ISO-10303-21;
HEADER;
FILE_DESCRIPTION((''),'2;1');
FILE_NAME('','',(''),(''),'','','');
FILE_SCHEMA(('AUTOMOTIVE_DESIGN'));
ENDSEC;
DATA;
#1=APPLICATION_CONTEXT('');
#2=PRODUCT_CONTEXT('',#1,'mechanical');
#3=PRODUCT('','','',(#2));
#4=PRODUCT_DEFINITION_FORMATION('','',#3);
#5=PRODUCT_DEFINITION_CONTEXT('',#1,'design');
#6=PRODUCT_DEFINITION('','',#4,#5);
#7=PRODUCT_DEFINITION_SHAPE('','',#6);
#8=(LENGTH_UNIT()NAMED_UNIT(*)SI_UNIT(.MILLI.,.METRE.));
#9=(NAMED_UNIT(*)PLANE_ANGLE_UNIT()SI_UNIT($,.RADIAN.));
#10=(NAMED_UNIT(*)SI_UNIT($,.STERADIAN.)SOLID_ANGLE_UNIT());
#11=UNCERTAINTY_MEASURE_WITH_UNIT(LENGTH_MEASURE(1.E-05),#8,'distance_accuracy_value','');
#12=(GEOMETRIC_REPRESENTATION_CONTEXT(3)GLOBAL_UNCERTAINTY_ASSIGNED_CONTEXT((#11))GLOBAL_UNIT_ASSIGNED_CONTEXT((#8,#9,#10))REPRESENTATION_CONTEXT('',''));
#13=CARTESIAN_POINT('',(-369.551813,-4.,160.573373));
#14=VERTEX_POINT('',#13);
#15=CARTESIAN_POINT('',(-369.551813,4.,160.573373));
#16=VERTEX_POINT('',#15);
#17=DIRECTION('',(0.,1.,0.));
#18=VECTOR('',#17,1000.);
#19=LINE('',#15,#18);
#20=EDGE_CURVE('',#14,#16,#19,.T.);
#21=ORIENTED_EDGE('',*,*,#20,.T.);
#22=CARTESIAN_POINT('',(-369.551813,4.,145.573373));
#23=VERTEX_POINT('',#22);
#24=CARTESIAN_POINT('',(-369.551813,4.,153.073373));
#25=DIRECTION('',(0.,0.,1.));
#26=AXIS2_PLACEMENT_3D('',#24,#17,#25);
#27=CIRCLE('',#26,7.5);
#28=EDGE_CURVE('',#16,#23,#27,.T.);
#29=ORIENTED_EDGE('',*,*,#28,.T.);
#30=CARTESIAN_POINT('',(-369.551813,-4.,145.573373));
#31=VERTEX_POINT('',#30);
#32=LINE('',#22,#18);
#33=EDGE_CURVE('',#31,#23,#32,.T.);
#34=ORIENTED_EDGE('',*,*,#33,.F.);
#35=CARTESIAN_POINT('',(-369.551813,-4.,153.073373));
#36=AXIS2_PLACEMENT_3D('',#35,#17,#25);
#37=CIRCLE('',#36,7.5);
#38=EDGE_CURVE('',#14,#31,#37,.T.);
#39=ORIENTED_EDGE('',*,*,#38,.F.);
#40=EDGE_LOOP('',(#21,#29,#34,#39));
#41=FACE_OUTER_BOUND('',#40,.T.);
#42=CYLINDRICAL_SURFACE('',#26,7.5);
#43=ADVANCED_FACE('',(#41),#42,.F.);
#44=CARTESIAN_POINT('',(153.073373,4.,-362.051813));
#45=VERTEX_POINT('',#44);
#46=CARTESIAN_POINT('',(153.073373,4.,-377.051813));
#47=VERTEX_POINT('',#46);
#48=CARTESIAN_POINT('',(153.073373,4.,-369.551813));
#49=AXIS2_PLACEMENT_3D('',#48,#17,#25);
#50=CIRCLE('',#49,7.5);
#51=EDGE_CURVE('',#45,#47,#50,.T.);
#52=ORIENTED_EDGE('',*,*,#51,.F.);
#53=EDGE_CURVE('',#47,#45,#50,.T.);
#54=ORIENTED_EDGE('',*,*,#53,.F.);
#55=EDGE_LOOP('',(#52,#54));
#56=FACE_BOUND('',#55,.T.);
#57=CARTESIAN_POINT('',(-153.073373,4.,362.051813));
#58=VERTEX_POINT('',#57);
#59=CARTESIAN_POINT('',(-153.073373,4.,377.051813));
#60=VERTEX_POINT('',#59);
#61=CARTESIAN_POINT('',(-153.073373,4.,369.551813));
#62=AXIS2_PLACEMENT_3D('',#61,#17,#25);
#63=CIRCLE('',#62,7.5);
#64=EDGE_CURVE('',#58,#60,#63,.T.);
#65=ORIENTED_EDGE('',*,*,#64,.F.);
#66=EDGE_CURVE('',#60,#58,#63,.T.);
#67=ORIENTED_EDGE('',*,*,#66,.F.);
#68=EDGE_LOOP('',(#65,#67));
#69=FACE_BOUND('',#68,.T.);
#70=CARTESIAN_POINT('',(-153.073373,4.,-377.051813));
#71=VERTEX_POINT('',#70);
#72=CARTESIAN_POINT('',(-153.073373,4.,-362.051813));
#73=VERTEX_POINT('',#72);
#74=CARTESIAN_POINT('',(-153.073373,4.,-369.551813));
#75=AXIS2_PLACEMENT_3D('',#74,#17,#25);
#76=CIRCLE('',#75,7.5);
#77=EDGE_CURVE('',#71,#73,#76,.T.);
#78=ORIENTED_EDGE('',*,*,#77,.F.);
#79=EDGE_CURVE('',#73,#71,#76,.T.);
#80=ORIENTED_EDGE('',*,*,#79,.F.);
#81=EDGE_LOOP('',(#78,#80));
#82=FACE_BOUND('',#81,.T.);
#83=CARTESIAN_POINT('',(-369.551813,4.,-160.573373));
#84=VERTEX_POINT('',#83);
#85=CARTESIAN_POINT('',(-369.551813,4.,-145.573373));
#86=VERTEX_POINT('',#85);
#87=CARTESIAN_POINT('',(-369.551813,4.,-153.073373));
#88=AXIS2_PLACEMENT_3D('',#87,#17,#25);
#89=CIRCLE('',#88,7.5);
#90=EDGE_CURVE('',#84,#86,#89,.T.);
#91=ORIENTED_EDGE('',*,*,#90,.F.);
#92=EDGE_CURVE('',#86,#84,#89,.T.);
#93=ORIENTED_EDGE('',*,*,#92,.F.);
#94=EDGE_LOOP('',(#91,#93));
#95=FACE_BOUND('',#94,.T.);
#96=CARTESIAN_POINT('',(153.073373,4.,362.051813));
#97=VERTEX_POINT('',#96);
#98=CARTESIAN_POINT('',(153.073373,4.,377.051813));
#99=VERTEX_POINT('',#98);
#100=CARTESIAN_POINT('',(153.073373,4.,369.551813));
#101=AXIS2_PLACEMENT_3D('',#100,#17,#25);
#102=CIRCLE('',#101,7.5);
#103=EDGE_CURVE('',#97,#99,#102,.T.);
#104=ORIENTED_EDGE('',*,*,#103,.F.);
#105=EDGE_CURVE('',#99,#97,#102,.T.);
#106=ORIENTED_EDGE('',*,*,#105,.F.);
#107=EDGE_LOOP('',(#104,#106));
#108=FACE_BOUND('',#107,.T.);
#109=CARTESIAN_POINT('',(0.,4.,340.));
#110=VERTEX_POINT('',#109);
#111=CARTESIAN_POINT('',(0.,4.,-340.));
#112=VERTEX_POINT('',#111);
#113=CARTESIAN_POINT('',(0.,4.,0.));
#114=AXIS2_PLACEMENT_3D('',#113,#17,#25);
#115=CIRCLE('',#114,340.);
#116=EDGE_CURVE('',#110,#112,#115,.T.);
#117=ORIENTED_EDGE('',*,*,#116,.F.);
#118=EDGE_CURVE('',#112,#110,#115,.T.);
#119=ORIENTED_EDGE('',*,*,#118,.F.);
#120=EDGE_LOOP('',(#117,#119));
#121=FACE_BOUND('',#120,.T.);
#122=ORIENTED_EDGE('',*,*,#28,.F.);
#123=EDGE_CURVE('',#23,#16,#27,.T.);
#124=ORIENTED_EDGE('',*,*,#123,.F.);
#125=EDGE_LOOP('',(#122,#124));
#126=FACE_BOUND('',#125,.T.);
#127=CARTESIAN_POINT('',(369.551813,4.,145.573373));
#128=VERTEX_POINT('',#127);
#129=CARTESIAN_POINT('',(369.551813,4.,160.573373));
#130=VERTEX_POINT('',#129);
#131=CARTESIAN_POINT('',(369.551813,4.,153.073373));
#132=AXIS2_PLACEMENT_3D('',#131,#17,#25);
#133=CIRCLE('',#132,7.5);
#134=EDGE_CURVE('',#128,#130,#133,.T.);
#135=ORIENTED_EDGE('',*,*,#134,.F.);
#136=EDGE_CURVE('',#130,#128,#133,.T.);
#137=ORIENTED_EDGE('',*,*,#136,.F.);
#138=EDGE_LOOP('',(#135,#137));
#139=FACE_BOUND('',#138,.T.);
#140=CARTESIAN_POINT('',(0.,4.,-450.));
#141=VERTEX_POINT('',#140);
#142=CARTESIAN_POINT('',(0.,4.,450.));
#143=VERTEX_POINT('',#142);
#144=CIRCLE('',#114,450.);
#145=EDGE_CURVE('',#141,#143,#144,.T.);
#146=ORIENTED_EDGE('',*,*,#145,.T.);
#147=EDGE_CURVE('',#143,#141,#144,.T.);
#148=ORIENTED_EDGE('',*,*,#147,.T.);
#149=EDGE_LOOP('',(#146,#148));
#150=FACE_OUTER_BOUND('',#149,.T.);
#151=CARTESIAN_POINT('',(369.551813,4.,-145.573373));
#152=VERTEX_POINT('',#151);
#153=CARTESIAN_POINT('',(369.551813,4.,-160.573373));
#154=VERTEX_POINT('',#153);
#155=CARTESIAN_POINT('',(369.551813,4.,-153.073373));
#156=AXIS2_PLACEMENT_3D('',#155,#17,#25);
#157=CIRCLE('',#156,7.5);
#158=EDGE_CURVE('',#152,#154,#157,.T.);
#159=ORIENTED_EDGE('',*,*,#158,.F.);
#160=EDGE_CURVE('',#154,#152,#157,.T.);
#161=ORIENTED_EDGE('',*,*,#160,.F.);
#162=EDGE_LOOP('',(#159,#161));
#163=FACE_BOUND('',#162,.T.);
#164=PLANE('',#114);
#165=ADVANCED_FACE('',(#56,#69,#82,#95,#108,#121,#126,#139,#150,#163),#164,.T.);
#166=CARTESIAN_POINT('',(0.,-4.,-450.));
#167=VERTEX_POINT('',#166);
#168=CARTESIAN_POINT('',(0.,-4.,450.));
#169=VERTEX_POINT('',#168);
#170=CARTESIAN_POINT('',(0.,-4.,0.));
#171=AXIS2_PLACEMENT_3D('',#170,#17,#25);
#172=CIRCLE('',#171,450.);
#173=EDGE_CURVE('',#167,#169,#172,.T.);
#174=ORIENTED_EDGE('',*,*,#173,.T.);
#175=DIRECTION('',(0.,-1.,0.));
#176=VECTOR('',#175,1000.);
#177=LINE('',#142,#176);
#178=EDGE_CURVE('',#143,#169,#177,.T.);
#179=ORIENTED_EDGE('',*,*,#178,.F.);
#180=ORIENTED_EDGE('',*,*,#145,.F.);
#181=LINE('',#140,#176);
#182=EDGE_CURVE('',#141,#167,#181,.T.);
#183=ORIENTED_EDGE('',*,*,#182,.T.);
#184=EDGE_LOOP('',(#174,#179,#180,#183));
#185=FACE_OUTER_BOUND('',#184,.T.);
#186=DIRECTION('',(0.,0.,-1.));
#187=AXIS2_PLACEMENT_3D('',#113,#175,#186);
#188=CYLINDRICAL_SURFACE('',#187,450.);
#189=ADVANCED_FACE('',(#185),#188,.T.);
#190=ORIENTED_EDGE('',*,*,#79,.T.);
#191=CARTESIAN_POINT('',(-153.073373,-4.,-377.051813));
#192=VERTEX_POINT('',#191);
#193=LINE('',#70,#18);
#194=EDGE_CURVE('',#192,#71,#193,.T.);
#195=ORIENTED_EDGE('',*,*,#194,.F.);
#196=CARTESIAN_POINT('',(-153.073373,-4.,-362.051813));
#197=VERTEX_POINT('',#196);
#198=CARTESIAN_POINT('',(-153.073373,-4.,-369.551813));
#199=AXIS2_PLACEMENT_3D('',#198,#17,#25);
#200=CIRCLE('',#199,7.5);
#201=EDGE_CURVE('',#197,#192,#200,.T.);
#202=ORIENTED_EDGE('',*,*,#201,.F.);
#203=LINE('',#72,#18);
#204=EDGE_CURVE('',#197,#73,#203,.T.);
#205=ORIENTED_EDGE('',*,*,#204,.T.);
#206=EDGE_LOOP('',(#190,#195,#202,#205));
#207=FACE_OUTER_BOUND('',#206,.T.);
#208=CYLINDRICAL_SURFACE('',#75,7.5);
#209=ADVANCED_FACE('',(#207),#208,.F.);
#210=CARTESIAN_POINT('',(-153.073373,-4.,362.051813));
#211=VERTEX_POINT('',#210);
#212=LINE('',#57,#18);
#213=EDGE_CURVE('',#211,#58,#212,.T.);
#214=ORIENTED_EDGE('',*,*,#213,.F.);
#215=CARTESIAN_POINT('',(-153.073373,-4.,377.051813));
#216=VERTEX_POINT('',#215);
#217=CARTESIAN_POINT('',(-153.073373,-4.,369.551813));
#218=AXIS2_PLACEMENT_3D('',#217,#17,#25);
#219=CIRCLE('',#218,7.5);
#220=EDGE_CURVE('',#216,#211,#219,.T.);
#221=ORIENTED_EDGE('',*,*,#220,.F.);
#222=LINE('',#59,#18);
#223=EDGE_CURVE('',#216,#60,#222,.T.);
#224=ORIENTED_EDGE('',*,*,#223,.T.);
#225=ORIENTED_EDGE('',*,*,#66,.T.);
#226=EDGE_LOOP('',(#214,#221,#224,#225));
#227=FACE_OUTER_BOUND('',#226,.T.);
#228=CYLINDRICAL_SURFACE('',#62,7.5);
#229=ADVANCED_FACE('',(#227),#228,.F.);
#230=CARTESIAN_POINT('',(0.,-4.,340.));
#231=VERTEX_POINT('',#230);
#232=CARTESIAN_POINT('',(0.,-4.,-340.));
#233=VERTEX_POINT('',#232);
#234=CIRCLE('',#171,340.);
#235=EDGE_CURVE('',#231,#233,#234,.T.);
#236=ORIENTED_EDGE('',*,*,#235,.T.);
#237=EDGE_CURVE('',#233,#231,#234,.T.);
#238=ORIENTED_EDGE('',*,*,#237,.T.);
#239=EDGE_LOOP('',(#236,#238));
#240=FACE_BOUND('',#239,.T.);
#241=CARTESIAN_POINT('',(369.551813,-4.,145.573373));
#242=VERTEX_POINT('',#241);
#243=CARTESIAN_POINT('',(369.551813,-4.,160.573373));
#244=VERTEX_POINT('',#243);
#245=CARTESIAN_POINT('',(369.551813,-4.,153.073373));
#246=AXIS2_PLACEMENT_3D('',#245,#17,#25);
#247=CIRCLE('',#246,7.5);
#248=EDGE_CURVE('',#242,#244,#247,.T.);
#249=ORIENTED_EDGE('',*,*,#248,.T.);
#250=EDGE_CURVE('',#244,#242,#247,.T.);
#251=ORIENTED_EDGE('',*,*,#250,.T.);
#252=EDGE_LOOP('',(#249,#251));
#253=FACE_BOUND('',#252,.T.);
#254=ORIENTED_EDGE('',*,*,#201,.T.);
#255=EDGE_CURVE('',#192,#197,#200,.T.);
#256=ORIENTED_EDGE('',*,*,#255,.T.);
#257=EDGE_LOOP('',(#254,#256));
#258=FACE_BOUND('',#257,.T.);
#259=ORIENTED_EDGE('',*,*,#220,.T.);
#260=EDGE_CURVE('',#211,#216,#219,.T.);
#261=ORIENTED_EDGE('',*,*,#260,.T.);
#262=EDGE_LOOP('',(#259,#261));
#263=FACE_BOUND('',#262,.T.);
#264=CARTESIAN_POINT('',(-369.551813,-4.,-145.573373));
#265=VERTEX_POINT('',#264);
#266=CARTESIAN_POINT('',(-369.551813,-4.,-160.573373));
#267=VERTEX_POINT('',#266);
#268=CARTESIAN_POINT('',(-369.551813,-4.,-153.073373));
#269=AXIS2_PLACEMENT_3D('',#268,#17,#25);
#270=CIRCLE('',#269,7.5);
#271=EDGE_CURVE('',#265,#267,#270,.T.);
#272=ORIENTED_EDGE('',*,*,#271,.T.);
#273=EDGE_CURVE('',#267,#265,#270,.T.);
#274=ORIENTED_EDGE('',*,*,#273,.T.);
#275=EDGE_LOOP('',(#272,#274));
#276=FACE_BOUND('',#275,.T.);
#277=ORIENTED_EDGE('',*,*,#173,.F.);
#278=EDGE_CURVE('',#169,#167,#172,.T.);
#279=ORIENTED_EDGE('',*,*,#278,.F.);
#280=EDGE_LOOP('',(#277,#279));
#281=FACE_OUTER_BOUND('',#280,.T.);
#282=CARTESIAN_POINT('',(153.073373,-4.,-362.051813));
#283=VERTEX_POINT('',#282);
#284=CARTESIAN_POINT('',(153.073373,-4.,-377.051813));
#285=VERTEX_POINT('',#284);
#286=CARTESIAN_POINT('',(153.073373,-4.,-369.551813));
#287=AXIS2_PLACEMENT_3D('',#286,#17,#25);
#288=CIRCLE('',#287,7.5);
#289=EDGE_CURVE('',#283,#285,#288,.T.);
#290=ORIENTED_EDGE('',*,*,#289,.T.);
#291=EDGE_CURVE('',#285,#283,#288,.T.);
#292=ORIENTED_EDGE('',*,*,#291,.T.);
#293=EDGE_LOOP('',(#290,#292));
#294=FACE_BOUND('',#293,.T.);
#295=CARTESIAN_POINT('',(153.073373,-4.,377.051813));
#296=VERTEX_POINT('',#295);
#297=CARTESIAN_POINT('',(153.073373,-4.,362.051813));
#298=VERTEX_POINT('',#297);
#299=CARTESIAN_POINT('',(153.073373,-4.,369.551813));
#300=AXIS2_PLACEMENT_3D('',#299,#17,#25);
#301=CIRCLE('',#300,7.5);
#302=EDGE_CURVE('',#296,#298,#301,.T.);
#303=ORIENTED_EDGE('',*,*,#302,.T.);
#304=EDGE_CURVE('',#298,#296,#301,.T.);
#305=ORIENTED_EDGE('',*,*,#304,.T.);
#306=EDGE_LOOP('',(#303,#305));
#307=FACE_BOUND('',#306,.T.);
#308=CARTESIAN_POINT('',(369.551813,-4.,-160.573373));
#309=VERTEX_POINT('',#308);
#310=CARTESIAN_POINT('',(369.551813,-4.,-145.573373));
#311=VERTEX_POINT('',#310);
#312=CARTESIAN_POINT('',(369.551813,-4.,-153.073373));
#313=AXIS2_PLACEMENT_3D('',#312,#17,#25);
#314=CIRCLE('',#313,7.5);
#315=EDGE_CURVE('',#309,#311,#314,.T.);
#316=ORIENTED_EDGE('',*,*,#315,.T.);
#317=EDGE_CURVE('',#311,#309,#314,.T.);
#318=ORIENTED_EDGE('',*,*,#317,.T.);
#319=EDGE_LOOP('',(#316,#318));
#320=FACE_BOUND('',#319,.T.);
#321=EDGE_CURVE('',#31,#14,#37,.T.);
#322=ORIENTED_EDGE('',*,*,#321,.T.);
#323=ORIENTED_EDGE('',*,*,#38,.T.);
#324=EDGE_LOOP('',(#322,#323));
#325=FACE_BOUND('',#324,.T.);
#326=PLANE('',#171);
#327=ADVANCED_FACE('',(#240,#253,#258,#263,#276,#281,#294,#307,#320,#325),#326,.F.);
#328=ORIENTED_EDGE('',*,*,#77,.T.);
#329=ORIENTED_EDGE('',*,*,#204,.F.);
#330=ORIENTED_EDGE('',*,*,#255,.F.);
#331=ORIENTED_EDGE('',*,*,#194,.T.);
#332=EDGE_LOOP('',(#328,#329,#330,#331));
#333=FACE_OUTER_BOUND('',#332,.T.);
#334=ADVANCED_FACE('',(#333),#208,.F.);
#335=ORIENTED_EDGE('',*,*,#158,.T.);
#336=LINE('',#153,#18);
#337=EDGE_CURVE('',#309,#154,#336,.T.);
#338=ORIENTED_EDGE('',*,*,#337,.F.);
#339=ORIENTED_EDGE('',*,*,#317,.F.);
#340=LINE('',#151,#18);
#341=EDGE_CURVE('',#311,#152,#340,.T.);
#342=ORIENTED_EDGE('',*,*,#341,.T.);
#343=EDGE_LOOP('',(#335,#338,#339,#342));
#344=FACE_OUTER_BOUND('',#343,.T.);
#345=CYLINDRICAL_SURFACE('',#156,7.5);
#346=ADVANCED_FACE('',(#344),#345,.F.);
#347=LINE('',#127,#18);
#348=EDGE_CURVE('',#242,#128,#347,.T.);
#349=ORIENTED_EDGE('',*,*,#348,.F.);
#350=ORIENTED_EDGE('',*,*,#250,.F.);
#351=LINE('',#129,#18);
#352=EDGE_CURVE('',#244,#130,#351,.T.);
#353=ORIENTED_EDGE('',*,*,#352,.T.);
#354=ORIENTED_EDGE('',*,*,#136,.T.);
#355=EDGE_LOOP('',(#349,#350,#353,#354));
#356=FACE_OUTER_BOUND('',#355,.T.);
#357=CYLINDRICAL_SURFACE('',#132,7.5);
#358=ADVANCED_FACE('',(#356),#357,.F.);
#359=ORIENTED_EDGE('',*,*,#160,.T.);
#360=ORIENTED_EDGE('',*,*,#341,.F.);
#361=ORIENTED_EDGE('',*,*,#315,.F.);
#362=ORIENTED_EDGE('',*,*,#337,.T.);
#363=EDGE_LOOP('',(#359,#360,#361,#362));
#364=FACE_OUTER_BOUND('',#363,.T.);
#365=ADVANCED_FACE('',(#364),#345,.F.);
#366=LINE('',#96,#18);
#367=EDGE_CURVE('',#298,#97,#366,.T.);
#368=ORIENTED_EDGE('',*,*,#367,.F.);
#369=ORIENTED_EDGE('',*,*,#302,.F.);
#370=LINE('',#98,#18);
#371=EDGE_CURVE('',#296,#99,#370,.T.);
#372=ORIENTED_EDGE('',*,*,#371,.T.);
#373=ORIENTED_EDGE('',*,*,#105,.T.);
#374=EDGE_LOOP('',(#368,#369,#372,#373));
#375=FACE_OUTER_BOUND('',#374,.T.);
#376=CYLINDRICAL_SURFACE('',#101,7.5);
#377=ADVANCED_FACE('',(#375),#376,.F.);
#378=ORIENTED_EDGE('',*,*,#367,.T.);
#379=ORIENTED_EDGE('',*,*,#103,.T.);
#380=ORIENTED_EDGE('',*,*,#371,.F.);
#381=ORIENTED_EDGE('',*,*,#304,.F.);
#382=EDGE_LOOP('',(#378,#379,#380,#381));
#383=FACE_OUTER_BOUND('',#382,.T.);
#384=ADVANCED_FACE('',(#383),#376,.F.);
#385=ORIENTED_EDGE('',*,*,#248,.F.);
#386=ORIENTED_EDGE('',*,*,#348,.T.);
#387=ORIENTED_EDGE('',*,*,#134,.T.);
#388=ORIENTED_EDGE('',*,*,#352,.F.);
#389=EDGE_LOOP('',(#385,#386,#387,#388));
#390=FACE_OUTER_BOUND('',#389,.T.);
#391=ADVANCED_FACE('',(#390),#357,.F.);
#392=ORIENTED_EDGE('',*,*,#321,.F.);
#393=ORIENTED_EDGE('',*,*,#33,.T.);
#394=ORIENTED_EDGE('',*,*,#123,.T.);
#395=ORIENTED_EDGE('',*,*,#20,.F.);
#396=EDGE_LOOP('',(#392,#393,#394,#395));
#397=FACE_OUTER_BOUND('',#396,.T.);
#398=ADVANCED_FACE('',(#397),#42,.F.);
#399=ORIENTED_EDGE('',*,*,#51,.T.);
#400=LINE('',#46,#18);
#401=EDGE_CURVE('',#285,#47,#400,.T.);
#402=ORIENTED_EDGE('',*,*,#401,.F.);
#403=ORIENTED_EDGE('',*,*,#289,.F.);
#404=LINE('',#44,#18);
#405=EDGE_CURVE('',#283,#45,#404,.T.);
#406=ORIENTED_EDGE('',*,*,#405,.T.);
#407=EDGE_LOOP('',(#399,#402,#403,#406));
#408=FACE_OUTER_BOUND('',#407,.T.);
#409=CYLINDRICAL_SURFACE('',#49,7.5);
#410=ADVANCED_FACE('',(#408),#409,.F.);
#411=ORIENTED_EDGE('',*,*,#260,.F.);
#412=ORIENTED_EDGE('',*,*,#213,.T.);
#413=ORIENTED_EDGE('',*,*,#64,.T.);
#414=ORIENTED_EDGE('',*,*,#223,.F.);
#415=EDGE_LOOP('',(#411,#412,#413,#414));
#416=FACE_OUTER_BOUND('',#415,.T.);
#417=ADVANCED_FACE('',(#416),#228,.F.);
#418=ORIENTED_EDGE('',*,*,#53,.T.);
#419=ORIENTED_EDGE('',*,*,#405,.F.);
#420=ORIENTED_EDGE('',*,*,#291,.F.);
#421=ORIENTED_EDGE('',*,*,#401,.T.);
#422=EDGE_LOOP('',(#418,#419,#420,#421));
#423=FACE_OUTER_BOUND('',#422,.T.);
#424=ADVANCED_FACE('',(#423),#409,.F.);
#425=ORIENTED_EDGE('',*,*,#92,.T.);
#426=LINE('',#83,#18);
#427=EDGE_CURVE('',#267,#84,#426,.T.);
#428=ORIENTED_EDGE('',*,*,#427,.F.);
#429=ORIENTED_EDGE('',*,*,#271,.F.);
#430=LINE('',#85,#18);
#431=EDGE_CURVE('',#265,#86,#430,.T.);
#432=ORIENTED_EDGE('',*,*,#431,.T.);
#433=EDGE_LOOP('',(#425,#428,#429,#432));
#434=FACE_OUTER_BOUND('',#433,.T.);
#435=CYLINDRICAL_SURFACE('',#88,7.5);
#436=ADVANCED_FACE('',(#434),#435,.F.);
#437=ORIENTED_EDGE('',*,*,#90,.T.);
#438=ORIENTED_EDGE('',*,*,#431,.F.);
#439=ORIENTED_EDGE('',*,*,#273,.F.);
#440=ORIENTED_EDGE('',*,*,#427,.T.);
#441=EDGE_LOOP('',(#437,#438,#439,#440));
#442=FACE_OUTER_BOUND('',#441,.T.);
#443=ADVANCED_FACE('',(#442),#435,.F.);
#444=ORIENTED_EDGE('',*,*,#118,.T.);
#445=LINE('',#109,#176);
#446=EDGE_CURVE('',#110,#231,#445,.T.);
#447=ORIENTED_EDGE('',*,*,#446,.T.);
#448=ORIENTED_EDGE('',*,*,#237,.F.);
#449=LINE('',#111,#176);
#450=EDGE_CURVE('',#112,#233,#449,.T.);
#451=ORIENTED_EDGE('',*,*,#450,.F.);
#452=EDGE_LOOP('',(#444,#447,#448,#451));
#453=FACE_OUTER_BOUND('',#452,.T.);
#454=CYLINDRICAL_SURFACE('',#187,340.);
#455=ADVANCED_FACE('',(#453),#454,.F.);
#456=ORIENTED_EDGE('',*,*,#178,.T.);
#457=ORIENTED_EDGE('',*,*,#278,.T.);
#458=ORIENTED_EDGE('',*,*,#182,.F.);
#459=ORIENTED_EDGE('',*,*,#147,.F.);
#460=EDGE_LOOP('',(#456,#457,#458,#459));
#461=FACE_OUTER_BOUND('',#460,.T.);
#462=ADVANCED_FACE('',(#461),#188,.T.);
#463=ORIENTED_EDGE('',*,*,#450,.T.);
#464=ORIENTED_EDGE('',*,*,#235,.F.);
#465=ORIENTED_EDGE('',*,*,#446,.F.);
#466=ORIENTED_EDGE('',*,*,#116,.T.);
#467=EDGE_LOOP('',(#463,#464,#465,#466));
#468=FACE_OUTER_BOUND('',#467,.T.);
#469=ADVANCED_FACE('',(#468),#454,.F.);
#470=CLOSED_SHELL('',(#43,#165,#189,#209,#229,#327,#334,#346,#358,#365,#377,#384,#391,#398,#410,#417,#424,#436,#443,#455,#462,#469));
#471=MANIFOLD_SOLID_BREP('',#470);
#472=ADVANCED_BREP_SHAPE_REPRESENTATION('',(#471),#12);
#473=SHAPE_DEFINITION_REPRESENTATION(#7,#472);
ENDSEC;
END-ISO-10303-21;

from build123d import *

# Parameters (mm, degrees)
SKETCH1_R                  = 450
SKETCH1_R_2                = 340
BOSS_EXTRUDE1_DEPTH        = 4
F_15_0_15_DIAMETER_HOLE1_D = 15


with BuildPart() as part:
    # Sketch1 → Boss-Extrude1 (new, symmetric)
    with BuildSketch(Plane(origin=(0, 0, 0), x_dir=(1, 0, 0), z_dir=(0, 1, 0))):
        with Locations(Location((0, 0, 0), (0, 0, 270))):
            Circle(SKETCH1_R)
        with Locations(Location((0, 0, 0), (0, 0, 270))):
            Circle(SKETCH1_R_2, mode=Mode.SUBTRACT)
    extrude(amount=BOSS_EXTRUDE1_DEPTH, both=True)

    # Ø15.0 (15) Diameter Hole1 (through all)
    with Locations(Plane(origin=(0, 4, 0), x_dir=(1, 0, 0), z_dir=(0, 1, 0))):
        with Locations((153.073372946, 369.551813005), (369.551813005, 153.073372946), (369.551813005, -153.073372946), (153.073372946, -369.551813005), (-153.073372946, -369.551813005), (-369.551813005, -153.073372946), (-369.551813005, 153.073372946), (-153.073372946, 369.551813005)):
            Hole(F_15_0_15_DIAMETER_HOLE1_D / 2)


solid = part.part
